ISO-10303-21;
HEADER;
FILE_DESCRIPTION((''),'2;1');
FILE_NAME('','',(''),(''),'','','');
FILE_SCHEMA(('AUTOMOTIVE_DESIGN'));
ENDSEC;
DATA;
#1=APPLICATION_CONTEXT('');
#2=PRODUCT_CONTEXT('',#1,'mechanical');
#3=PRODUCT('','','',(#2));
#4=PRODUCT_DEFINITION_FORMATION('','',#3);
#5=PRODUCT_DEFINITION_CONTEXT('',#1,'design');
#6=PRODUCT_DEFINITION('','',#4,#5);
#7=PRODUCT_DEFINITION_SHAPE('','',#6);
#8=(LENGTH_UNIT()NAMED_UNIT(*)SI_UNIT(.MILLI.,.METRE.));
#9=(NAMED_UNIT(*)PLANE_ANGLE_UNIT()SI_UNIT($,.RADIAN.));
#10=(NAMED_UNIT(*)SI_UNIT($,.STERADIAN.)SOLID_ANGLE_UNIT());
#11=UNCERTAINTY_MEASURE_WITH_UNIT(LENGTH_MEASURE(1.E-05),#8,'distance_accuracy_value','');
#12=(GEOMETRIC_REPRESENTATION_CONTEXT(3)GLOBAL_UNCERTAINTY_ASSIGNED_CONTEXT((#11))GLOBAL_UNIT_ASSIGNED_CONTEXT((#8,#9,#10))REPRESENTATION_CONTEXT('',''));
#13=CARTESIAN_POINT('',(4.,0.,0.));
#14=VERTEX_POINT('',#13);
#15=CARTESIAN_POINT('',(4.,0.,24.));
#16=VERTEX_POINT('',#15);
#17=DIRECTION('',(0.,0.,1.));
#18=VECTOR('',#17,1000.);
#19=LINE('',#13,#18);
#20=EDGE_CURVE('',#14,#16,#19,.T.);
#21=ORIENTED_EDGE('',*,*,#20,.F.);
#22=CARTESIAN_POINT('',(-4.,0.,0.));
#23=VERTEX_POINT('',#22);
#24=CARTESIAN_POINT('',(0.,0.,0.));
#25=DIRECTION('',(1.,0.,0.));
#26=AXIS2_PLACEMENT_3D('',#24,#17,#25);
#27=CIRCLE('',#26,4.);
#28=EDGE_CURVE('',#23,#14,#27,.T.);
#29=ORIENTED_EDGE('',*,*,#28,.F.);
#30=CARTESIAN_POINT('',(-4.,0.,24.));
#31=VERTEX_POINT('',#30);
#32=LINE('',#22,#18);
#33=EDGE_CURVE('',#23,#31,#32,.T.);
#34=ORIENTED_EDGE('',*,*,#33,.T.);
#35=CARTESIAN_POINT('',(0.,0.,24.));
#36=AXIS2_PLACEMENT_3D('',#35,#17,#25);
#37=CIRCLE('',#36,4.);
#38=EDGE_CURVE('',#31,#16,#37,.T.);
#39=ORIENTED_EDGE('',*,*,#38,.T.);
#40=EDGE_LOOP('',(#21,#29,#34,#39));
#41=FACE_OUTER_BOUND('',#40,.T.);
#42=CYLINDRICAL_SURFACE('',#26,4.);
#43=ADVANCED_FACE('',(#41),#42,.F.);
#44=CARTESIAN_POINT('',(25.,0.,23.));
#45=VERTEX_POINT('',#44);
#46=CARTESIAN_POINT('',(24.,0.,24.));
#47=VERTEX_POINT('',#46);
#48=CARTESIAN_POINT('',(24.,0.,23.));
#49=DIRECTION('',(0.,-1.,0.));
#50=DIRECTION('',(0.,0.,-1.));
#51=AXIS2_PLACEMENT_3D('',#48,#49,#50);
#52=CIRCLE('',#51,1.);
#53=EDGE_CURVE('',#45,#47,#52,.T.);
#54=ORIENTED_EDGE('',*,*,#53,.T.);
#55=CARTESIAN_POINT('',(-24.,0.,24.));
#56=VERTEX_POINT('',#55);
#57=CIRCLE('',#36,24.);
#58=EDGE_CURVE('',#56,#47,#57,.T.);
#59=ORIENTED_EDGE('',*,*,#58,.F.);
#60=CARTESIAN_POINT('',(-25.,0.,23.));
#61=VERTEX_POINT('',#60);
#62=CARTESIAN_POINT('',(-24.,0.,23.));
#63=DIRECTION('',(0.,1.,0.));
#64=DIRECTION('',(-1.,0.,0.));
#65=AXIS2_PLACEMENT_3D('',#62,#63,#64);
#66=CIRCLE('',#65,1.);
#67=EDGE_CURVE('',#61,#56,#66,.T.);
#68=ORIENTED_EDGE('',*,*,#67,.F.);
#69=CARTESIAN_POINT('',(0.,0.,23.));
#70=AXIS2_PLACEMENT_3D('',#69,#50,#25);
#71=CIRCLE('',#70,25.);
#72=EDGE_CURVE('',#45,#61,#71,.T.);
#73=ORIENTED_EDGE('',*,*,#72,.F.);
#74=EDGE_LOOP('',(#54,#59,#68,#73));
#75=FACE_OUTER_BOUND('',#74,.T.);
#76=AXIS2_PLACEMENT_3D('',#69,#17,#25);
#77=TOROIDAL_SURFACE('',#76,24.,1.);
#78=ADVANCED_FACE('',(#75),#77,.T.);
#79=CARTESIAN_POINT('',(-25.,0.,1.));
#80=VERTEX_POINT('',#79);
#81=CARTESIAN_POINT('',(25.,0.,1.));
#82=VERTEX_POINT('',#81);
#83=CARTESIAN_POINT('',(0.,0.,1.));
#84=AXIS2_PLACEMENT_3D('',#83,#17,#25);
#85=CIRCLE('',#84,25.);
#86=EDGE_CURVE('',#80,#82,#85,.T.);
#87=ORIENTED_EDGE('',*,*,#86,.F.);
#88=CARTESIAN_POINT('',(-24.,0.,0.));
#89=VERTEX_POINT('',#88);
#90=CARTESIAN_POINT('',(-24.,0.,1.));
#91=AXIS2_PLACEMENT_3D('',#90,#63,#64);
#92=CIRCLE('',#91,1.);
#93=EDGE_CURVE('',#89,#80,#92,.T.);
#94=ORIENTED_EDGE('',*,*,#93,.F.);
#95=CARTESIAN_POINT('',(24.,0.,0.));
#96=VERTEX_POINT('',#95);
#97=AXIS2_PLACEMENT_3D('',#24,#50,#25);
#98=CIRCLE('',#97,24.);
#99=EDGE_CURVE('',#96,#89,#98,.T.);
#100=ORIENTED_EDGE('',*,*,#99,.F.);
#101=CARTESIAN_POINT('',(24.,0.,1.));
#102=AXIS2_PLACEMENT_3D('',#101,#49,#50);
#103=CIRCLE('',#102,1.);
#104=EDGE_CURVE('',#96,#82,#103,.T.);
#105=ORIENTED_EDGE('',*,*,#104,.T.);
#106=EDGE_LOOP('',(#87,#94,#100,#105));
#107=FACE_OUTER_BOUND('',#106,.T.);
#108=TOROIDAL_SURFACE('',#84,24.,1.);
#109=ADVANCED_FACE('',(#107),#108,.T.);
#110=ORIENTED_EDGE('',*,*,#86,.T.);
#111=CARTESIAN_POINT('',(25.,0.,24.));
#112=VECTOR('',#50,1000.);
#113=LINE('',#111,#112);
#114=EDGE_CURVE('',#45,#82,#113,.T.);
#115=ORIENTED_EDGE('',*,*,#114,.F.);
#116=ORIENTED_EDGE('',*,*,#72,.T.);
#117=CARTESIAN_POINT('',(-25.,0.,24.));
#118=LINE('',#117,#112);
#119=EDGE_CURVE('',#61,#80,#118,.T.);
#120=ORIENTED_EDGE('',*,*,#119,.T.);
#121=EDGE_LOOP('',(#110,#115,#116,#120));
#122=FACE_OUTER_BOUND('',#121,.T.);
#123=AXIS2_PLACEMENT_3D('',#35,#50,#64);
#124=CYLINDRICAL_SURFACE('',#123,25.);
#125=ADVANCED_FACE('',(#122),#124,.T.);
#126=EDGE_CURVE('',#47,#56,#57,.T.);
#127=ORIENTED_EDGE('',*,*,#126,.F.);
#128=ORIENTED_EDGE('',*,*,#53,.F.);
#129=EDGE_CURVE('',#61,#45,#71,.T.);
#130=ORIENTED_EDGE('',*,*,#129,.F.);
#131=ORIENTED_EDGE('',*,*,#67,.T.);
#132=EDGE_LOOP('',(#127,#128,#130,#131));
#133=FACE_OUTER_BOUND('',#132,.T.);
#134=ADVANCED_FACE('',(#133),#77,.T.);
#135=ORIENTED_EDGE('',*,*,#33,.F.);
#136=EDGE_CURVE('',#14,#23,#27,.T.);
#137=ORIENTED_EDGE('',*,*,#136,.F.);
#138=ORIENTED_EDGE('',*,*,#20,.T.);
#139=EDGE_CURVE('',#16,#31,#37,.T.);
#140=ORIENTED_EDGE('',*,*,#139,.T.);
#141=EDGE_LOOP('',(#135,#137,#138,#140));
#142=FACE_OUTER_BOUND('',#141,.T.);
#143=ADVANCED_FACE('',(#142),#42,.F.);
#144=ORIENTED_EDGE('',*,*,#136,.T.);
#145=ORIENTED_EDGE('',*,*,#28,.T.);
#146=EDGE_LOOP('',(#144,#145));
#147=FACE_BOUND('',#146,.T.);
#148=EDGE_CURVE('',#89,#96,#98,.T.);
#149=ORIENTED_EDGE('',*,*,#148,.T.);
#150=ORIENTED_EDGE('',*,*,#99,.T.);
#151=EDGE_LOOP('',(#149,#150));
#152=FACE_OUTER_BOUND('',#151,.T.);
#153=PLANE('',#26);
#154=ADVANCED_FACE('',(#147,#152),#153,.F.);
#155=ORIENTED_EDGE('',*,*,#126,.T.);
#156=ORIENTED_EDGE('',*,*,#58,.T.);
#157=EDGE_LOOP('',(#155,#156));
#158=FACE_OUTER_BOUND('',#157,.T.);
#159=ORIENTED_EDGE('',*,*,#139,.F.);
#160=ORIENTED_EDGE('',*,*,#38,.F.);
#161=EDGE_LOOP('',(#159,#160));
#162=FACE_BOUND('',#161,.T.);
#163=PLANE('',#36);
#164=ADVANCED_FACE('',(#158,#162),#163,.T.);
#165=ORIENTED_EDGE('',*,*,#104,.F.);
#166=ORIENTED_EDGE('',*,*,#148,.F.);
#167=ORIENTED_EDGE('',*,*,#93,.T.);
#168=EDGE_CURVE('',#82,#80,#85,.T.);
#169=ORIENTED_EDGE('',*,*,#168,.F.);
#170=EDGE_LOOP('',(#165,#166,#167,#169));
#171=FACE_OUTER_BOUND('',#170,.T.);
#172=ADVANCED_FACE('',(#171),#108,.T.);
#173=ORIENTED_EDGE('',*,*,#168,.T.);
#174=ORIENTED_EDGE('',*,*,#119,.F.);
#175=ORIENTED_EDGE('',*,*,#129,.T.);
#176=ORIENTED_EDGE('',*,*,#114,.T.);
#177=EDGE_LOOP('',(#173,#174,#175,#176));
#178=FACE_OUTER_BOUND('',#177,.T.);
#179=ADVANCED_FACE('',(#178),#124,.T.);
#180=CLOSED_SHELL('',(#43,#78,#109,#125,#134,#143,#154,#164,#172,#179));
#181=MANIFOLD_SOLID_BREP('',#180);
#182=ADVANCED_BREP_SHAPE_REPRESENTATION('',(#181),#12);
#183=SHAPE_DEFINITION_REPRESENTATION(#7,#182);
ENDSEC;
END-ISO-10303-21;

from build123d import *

# Parameters (mm, degrees)
SKETCH_1_R          = 25
EXTRUDE_1_DEPTH     = 24
SKETCH_2_R          = 4
CUT_EXTRUDE_1_DEPTH = 24
FILLET_1_R          = 1


with BuildPart() as part:
    # 草图1 → 凸台-拉伸1 (new body)
    with BuildSketch(Plane.XY):
        Circle(SKETCH_1_R)
    extrude(amount=EXTRUDE_1_DEPTH)

    # 草图2 → 切除-拉伸1 (cut)
    with BuildSketch(Plane.XY.offset(24)):
        Circle(SKETCH_2_R)
    extrude(amount=-CUT_EXTRUDE_1_DEPTH, mode=Mode.SUBTRACT)

    # 圆角1
    fillet_1_edges = [part.edges().sort_by_distance(p)[0] for p in [
        (-25, 0, 0),
        (-25, 0, 24),
    ]]
    fillet(fillet_1_edges, radius=FILLET_1_R)


solid = part.part
